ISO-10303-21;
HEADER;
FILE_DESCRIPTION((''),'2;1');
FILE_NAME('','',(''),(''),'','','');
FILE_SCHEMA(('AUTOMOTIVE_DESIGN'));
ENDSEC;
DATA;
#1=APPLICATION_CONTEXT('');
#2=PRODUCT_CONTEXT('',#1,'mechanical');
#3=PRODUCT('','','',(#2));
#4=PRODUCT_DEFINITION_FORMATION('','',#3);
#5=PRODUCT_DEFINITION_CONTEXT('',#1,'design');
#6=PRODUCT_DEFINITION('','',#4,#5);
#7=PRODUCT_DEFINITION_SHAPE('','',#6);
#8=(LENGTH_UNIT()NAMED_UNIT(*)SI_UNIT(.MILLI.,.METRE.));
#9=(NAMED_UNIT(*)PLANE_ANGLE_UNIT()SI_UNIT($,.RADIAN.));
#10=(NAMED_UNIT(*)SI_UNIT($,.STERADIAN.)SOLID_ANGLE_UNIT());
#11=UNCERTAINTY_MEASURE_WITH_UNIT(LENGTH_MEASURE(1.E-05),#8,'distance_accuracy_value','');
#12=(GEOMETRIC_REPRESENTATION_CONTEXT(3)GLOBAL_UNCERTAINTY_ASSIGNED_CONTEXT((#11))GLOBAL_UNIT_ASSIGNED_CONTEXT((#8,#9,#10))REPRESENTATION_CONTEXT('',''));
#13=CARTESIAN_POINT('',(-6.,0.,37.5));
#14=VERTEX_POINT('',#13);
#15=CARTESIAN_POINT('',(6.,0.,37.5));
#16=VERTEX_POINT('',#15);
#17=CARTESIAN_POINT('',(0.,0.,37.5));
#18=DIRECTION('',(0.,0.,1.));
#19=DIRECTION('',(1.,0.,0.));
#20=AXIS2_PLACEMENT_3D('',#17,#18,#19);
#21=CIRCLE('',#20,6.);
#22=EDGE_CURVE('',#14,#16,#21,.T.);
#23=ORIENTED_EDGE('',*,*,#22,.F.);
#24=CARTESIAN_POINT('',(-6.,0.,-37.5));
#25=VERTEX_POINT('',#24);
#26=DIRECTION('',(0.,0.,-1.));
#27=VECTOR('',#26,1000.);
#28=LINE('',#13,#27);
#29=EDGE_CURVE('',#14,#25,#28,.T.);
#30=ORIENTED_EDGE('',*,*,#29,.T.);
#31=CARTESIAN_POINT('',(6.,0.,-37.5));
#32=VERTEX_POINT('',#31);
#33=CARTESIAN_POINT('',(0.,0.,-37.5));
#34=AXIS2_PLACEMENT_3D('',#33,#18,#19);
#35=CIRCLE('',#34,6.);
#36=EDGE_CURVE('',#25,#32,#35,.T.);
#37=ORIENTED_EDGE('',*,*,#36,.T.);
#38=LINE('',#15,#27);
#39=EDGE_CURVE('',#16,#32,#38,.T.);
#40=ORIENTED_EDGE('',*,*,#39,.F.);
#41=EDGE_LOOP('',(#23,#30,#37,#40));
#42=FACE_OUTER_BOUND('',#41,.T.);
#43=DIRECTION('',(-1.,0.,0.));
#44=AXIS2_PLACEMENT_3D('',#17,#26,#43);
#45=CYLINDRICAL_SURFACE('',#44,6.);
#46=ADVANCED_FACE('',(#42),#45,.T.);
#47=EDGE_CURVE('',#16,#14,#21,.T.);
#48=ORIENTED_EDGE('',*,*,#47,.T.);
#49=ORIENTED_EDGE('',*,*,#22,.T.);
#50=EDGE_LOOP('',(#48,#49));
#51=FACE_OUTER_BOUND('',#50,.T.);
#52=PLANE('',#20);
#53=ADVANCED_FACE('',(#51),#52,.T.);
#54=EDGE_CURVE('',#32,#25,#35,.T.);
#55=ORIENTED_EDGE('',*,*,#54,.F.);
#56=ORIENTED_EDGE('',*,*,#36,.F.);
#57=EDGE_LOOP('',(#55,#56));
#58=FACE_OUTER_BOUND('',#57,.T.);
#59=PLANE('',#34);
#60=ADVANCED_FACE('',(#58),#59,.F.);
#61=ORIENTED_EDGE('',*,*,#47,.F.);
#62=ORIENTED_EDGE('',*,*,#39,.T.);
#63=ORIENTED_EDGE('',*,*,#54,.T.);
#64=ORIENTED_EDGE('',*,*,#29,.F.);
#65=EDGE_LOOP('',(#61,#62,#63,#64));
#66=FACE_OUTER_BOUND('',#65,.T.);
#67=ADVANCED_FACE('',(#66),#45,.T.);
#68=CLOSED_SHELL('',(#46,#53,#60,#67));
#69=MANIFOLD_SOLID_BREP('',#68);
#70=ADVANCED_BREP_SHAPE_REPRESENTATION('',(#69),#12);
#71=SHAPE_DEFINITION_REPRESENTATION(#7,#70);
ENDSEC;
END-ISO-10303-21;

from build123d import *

# Parameters (mm, degrees)
SKETCH_1_R      = 6
EXTRUDE_1_DEPTH = 37.5


with BuildPart() as part:
    # 草图1 → 凸台-拉伸1 (new, symmetric)
    with BuildSketch(Plane.XY):
        Circle(SKETCH_1_R)
    extrude(amount=EXTRUDE_1_DEPTH, both=True)


solid = part.part
